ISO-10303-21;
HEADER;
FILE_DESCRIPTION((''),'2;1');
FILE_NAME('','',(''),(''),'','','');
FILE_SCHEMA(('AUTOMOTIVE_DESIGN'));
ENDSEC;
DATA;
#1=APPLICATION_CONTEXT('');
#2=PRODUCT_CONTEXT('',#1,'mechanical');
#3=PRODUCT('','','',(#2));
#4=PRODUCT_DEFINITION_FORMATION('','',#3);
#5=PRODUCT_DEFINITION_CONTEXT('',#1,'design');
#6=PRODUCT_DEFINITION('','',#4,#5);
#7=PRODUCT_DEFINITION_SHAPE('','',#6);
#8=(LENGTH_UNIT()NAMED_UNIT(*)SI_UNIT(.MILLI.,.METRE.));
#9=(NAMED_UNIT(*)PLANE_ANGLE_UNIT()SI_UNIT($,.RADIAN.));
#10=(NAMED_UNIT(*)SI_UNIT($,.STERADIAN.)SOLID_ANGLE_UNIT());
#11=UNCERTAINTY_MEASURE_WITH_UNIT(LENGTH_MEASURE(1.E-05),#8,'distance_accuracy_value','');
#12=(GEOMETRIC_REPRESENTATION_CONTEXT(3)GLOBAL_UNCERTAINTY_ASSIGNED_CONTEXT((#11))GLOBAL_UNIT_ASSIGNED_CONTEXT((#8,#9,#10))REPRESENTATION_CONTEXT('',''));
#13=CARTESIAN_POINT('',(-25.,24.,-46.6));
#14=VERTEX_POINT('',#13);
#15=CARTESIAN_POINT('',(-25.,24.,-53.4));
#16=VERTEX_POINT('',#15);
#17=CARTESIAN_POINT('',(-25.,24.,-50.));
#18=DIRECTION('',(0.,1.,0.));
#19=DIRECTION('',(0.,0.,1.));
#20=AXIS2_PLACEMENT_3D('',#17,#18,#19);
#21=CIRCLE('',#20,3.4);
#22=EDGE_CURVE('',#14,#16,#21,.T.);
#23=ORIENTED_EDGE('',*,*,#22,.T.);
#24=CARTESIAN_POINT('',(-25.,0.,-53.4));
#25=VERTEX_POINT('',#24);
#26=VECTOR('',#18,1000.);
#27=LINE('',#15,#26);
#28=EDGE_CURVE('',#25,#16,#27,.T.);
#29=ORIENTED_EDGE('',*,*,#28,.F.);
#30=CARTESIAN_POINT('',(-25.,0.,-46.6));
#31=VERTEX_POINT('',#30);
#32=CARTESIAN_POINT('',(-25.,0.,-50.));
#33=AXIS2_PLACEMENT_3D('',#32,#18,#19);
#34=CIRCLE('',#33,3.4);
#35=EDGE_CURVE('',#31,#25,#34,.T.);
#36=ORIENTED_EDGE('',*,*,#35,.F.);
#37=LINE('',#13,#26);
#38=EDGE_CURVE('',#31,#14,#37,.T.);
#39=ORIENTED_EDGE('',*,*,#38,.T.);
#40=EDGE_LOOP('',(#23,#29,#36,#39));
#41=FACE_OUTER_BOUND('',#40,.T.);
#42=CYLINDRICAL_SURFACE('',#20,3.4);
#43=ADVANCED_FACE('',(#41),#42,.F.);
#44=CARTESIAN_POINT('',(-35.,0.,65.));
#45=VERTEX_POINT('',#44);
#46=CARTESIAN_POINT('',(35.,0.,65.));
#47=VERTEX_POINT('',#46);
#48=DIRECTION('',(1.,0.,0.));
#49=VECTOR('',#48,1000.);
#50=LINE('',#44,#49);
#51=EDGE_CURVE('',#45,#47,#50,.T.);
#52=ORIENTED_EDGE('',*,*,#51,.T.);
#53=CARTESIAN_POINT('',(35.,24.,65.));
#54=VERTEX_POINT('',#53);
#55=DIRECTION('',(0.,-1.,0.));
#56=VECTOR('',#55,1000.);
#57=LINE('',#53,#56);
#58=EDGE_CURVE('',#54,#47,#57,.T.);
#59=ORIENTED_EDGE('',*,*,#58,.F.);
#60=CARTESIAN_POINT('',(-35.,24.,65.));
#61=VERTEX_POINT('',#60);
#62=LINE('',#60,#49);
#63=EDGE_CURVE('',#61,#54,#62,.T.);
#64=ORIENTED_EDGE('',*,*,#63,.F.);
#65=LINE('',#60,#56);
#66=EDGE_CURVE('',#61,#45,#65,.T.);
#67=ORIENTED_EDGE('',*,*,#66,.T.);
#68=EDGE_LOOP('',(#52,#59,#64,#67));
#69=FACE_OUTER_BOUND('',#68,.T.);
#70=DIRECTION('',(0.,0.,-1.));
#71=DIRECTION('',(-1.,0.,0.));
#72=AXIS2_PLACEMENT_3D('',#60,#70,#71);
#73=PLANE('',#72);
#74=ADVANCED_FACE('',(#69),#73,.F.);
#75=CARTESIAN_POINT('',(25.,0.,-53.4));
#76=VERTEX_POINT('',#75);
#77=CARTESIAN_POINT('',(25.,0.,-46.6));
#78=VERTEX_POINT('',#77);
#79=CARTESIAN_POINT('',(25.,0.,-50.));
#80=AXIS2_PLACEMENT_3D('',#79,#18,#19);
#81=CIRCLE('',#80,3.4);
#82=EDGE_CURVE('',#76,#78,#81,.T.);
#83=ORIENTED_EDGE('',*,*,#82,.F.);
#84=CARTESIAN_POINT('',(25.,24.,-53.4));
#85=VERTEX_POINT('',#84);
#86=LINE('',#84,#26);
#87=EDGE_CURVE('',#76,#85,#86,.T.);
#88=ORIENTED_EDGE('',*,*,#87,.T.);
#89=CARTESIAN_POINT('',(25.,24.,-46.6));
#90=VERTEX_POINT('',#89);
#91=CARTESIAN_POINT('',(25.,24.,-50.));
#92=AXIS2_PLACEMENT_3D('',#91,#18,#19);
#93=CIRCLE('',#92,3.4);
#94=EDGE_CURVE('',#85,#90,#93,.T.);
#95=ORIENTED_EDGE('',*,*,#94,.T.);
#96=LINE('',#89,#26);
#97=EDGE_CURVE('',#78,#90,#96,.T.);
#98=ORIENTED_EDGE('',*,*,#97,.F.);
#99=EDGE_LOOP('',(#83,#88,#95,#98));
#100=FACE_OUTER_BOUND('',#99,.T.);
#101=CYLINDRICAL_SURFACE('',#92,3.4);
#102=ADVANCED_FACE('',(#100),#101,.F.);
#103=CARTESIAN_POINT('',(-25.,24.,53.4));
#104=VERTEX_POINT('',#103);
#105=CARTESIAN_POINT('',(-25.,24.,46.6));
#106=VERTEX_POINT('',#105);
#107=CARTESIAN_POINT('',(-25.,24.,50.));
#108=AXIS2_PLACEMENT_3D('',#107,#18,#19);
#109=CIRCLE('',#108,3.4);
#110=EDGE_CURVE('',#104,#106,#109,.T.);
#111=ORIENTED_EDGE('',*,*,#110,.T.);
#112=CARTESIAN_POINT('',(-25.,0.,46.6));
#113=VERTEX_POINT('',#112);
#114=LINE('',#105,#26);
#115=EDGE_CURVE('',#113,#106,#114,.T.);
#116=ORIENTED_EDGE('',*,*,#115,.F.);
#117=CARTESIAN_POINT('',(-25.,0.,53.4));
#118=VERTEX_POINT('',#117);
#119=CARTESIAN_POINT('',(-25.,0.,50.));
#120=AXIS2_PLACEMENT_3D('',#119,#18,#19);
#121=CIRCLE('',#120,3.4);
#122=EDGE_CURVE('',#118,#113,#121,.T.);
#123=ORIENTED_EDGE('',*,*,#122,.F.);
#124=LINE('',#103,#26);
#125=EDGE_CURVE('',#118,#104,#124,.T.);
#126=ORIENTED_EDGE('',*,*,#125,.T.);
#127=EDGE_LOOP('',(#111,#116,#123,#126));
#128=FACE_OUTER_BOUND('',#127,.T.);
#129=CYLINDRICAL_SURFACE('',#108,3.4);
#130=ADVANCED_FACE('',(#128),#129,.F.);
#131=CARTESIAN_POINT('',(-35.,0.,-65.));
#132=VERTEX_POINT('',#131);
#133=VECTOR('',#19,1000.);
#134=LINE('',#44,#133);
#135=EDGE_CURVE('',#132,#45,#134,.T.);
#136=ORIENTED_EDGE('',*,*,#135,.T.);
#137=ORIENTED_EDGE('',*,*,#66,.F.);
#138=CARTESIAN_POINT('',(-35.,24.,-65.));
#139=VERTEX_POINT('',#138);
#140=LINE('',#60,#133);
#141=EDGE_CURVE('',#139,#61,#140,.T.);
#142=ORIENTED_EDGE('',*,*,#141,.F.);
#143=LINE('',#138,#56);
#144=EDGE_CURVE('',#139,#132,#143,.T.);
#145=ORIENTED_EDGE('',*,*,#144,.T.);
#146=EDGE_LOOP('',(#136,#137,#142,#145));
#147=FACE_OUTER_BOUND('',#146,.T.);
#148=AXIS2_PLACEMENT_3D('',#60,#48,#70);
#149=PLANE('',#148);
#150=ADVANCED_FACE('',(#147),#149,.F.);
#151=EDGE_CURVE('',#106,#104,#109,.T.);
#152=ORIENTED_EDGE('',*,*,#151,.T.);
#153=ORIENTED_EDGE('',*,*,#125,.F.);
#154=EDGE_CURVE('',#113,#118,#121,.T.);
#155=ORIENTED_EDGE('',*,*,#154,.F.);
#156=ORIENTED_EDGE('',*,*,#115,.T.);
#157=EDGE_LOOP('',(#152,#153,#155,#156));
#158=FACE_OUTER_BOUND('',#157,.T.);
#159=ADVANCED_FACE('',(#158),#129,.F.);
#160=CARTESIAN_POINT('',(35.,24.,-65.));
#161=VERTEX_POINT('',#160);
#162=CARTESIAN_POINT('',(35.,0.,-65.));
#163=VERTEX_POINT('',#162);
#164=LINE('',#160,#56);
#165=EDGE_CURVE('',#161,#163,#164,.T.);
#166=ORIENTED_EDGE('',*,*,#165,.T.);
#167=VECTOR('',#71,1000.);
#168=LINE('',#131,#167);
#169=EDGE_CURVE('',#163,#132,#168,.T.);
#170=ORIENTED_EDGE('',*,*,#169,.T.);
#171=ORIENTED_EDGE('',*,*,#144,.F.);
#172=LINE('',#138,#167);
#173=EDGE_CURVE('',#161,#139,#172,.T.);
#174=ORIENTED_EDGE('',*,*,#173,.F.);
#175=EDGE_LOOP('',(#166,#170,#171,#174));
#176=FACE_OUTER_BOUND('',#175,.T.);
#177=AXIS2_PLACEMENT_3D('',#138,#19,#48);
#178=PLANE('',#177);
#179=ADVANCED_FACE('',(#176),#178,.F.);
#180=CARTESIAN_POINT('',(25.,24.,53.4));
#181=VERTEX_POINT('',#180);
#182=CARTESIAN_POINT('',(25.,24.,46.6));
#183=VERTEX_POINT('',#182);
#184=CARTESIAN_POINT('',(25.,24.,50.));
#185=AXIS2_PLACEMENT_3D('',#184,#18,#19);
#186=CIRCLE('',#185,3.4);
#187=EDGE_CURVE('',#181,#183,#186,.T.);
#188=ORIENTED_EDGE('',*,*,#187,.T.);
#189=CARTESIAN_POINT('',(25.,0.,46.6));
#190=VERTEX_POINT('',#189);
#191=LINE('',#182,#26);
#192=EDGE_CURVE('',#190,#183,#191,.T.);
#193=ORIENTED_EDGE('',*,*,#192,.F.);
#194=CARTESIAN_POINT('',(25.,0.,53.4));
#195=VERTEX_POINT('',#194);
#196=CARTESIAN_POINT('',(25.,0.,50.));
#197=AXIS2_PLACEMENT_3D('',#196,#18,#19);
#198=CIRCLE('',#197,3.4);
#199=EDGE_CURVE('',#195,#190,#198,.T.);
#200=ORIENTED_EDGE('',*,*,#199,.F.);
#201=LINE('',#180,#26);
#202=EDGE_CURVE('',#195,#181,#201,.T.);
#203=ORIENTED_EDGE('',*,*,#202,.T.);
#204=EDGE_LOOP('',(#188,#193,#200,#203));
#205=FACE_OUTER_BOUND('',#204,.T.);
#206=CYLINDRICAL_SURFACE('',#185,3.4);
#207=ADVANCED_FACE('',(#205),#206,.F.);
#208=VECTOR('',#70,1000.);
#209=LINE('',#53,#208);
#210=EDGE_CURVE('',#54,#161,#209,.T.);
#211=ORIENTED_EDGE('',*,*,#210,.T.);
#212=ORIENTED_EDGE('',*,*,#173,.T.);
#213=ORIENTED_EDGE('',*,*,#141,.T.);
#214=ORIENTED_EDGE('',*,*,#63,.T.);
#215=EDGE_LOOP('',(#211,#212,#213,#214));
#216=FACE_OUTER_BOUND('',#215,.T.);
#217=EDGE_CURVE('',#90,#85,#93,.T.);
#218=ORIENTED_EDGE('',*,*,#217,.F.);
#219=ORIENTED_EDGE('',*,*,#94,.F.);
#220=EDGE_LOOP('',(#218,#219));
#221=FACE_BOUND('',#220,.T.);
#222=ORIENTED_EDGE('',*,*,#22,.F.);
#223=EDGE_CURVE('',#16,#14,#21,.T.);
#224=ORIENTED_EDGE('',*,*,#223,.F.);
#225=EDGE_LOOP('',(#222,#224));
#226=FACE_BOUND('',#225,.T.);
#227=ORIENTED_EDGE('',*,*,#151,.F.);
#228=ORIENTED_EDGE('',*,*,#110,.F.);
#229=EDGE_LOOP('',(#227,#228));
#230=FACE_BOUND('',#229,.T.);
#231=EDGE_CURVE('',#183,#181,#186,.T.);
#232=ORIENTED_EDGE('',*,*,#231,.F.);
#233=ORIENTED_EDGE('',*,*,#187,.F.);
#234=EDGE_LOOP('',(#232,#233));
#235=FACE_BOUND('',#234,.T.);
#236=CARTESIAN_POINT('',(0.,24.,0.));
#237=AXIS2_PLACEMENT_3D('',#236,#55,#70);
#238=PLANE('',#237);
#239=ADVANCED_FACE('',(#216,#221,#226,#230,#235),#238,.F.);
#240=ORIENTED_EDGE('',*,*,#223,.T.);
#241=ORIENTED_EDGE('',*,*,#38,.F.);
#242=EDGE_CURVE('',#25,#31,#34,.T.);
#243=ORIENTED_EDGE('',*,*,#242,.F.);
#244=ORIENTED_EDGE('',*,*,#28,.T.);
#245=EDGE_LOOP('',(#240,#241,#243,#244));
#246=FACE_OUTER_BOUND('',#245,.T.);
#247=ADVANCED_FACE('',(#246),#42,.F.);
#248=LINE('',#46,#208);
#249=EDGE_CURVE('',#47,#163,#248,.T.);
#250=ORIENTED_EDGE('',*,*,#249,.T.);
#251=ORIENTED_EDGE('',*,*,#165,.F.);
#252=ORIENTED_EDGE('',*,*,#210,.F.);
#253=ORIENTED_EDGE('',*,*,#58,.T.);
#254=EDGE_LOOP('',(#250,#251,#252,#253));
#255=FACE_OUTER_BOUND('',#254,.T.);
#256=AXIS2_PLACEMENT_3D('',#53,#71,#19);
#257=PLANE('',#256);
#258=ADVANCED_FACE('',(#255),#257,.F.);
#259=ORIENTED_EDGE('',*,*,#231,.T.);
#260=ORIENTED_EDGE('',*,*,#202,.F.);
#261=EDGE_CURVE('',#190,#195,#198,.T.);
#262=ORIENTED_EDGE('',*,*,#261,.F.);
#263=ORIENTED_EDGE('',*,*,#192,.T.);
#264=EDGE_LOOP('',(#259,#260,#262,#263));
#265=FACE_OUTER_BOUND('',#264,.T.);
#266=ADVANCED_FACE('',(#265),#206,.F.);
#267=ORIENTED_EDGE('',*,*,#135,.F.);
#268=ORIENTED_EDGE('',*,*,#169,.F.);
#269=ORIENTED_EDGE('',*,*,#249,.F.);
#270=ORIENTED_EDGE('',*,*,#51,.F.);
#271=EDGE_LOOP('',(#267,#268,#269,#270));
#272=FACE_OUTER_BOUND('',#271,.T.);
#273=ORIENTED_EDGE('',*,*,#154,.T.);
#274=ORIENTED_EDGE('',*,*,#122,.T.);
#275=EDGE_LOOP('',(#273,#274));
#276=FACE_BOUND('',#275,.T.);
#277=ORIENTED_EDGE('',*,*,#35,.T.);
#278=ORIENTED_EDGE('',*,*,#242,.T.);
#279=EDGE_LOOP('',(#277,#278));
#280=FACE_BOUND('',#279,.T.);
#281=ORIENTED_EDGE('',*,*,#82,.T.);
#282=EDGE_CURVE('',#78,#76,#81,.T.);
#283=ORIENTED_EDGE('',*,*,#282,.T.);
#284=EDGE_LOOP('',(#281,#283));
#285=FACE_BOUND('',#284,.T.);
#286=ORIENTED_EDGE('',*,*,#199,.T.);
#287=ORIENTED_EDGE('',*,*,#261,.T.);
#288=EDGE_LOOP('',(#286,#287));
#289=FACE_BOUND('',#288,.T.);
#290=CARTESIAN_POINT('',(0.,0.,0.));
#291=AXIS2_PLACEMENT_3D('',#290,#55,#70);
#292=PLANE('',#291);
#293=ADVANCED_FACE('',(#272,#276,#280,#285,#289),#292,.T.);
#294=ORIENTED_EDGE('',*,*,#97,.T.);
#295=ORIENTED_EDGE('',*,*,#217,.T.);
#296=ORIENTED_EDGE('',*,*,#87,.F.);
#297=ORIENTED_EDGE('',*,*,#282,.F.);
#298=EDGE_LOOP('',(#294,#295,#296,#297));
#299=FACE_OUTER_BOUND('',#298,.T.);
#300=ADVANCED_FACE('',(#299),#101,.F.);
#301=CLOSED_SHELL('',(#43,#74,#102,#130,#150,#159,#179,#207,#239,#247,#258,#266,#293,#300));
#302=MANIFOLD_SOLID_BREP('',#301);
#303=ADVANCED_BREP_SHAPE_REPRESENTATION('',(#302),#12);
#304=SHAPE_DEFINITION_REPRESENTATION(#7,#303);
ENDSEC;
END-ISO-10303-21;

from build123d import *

# Parameters (mm, degrees)
SKETCH_1_W         = 70
SKETCH_1_H         = 130
EXTRUDE_1_DEPTH    = 24
HOLE_WIZARD_M8_1_D = 6.8


with BuildPart() as part:
    # 草图1 → 凸台-拉伸1 (new body)
    with BuildSketch(Plane(origin=(0, 0, 0), x_dir=(1, 0, 0), z_dir=(0, 1, 0))):
        Rectangle(SKETCH_1_W, SKETCH_1_H)
    extrude(amount=EXTRUDE_1_DEPTH)

    # M8 螺纹孔1 (through all)
    with Locations(Plane(origin=(0, 24, 0), x_dir=(1, 0, 0), z_dir=(0, 1, 0))):
        with Locations((-25, -50), (-25, 50), (25, 50), (25, -50)):
            Hole(HOLE_WIZARD_M8_1_D / 2)


solid = part.part
